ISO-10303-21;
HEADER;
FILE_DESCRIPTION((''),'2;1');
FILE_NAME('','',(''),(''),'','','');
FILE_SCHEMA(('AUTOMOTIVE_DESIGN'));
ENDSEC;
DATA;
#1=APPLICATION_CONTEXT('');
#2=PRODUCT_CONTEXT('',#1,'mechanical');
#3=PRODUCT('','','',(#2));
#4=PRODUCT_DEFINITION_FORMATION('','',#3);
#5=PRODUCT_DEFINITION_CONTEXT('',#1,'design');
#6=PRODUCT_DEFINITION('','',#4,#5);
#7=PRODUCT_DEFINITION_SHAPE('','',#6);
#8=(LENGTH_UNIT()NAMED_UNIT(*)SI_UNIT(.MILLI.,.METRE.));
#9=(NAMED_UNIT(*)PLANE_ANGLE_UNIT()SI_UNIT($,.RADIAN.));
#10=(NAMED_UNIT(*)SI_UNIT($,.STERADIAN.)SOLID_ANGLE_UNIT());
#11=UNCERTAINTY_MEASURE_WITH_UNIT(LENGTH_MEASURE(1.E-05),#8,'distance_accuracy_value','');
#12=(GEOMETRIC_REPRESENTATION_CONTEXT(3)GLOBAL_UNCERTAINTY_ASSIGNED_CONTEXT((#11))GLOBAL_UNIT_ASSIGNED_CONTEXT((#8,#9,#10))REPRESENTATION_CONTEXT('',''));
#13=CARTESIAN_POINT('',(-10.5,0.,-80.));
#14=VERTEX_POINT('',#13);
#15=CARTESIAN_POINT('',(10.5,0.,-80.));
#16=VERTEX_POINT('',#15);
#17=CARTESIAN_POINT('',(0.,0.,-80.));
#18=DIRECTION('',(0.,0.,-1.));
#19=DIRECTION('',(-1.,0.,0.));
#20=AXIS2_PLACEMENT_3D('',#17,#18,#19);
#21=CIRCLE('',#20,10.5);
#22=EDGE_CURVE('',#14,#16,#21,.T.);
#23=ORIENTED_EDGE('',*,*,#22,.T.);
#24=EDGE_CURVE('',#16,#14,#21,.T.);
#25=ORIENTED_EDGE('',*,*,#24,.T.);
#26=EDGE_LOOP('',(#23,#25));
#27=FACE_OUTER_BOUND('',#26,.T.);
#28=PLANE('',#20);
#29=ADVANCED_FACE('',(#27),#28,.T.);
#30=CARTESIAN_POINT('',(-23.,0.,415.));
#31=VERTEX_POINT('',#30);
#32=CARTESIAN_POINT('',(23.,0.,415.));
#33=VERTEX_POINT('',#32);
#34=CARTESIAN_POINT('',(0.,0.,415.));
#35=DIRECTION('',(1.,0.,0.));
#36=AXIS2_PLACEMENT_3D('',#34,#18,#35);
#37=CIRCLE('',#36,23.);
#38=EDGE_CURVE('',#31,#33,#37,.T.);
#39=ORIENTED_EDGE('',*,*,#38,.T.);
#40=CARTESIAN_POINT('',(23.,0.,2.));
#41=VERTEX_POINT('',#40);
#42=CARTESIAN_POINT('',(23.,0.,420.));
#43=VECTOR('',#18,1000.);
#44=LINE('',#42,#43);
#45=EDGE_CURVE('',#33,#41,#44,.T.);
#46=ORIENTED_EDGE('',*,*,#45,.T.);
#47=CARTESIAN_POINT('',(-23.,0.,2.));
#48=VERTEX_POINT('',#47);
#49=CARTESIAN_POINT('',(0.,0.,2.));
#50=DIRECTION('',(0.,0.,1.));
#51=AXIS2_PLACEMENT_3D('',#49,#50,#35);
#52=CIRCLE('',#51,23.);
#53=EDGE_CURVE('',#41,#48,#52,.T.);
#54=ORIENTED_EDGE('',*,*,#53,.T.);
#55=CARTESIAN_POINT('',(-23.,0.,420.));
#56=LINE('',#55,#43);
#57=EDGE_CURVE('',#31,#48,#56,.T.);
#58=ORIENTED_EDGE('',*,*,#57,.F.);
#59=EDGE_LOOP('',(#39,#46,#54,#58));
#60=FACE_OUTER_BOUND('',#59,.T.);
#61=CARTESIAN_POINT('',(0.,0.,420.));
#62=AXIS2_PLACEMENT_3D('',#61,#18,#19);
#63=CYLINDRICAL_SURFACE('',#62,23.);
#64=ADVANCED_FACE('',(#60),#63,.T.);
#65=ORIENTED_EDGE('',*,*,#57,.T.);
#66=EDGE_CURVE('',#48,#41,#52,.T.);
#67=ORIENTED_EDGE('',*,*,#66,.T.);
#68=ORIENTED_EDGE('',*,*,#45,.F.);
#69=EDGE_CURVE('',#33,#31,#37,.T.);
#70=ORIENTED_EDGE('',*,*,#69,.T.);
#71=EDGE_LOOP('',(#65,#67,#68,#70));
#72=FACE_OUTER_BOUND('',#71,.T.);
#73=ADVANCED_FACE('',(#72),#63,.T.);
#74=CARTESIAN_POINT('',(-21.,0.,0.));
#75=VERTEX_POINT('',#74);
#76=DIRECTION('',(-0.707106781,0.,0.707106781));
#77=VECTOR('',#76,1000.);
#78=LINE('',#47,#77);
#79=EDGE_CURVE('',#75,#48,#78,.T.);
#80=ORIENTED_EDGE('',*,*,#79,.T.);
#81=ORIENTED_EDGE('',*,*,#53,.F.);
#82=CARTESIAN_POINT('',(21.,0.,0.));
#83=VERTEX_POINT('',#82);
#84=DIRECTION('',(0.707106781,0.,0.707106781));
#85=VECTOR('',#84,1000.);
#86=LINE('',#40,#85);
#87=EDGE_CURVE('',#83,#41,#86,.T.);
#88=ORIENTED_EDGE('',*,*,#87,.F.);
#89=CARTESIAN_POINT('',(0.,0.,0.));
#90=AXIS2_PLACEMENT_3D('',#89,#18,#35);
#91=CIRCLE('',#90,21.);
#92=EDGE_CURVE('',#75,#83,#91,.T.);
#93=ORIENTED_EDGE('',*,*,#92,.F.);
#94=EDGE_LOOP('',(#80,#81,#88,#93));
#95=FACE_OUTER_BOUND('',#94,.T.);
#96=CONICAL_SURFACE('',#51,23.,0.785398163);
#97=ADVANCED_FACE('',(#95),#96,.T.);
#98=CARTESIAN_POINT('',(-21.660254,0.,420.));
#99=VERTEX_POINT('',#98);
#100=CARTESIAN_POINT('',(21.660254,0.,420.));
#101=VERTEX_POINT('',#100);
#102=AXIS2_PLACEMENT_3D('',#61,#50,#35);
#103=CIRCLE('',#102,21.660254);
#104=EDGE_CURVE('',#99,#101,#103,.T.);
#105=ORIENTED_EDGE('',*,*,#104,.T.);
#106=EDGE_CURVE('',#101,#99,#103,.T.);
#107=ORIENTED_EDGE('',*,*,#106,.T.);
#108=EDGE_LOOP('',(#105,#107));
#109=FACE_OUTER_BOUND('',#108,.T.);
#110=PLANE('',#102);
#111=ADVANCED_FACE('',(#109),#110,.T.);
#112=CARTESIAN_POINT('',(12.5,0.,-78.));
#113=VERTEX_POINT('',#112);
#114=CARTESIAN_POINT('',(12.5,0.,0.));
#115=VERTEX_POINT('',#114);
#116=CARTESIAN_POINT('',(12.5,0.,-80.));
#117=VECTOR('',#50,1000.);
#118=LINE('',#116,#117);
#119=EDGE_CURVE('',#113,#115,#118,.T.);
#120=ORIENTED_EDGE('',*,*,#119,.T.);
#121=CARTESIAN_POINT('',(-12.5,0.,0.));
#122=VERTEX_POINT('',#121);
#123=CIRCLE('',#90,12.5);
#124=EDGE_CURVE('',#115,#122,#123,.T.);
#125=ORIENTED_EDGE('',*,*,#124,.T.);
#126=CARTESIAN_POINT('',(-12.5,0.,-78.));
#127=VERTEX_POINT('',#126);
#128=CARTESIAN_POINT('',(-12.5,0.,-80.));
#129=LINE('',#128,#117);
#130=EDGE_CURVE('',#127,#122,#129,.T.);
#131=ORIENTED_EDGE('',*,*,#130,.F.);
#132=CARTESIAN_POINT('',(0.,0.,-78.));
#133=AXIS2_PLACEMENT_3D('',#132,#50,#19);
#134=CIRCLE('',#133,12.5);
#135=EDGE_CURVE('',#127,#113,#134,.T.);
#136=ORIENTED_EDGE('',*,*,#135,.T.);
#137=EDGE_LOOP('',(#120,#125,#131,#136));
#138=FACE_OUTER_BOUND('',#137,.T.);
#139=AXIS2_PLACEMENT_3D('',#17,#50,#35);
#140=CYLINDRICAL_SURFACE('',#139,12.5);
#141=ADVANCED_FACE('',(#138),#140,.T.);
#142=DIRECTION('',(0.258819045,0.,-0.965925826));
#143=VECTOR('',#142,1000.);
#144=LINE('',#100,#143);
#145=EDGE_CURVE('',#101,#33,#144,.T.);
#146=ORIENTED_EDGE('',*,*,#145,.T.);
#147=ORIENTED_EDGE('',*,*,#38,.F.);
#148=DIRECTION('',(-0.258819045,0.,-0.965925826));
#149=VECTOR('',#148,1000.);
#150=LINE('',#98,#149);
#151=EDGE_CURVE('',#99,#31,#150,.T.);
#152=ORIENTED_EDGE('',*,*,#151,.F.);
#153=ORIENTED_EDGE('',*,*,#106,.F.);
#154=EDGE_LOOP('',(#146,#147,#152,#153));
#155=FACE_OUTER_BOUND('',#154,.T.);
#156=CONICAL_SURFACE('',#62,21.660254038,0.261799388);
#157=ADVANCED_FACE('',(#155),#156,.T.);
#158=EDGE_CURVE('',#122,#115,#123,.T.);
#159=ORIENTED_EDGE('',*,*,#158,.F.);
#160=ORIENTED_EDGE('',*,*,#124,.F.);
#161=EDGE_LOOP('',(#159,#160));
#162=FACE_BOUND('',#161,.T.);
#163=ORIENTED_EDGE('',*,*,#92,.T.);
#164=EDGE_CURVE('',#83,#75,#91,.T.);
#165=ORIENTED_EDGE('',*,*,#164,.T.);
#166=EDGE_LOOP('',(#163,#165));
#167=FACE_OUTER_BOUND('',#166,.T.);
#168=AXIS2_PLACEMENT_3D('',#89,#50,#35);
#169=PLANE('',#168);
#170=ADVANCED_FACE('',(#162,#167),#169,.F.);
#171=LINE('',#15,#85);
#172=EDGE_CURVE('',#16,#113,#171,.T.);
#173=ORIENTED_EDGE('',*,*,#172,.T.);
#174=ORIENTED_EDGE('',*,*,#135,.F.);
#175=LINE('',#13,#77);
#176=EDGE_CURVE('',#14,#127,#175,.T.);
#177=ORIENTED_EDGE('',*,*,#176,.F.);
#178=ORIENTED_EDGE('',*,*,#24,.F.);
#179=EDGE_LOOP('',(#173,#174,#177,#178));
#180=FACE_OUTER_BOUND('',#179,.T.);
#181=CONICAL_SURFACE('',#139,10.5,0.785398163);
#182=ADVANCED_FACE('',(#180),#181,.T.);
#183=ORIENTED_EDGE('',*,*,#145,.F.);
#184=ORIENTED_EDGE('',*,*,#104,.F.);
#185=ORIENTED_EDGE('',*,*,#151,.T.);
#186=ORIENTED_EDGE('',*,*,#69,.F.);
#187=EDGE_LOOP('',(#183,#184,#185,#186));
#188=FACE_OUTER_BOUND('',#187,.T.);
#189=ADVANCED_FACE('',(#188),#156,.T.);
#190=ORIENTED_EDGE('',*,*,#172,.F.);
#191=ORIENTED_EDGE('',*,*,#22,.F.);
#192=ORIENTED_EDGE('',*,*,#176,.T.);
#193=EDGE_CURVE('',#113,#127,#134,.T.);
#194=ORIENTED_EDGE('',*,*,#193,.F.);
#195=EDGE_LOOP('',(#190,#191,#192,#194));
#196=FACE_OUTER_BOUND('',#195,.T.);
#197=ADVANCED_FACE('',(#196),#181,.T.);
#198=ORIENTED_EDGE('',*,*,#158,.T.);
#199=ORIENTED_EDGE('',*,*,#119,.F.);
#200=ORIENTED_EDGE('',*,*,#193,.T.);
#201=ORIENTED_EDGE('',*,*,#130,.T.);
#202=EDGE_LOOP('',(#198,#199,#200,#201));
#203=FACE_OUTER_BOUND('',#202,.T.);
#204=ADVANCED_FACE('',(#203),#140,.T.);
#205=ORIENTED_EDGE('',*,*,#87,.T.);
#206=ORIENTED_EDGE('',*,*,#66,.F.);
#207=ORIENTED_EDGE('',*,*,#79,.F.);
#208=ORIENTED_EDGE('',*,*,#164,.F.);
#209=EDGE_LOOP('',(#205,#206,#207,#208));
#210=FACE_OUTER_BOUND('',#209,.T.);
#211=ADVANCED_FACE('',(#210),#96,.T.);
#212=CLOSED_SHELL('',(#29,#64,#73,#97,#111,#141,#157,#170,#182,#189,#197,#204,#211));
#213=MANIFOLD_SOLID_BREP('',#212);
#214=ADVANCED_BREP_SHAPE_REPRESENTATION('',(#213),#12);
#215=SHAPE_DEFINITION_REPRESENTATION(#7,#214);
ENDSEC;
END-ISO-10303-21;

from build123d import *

# Parameters (mm, degrees)
SKETCH1_R           = 23
BOSS_EXTRUDE1_DEPTH = 420
CHAMFER1_SIZE       = 5
CHAMFER1_SIZE2      = 1.339745962
SKETCH2_R           = 12.5
BOSS_EXTRUDE2_DEPTH = 80
CHAMFER2_SIZE       = 2


with BuildPart() as part:
    # Sketch1 → Boss-Extrude1 (new body)
    with BuildSketch(Plane.XY):
        Circle(SKETCH1_R)
    extrude(amount=BOSS_EXTRUDE1_DEPTH)

    # Chamfer1
    chamfer1_edges = [part.edges().sort_by_distance(p)[0] for p in [
        (-23, 0, 420),
    ]]
    chamfer1_side = [part.faces().sort_by_distance(p)[0] for p in [
        (-23, 0, 210),
    ]]
    chamfer(chamfer1_edges, length=CHAMFER1_SIZE, length2=CHAMFER1_SIZE2, reference=chamfer1_side[0])

    # Sketch2 → Boss-Extrude2 (add)
    with BuildSketch(Plane(origin=(0, 0, 0), x_dir=(-1, 0, 0), z_dir=(0, 0, -1))):
        with Locations(Location((0, 0, 0), (0, 0, 180))):
            Circle(SKETCH2_R)
    extrude(amount=BOSS_EXTRUDE2_DEPTH)

    # Chamfer2
    chamfer2_edges = [part.edges().sort_by_distance(p)[0] for p in [
        (-23, 0, 0),
        (-12.5, 0, -80),
    ]]
    chamfer(chamfer2_edges, length=CHAMFER2_SIZE)


solid = part.part
